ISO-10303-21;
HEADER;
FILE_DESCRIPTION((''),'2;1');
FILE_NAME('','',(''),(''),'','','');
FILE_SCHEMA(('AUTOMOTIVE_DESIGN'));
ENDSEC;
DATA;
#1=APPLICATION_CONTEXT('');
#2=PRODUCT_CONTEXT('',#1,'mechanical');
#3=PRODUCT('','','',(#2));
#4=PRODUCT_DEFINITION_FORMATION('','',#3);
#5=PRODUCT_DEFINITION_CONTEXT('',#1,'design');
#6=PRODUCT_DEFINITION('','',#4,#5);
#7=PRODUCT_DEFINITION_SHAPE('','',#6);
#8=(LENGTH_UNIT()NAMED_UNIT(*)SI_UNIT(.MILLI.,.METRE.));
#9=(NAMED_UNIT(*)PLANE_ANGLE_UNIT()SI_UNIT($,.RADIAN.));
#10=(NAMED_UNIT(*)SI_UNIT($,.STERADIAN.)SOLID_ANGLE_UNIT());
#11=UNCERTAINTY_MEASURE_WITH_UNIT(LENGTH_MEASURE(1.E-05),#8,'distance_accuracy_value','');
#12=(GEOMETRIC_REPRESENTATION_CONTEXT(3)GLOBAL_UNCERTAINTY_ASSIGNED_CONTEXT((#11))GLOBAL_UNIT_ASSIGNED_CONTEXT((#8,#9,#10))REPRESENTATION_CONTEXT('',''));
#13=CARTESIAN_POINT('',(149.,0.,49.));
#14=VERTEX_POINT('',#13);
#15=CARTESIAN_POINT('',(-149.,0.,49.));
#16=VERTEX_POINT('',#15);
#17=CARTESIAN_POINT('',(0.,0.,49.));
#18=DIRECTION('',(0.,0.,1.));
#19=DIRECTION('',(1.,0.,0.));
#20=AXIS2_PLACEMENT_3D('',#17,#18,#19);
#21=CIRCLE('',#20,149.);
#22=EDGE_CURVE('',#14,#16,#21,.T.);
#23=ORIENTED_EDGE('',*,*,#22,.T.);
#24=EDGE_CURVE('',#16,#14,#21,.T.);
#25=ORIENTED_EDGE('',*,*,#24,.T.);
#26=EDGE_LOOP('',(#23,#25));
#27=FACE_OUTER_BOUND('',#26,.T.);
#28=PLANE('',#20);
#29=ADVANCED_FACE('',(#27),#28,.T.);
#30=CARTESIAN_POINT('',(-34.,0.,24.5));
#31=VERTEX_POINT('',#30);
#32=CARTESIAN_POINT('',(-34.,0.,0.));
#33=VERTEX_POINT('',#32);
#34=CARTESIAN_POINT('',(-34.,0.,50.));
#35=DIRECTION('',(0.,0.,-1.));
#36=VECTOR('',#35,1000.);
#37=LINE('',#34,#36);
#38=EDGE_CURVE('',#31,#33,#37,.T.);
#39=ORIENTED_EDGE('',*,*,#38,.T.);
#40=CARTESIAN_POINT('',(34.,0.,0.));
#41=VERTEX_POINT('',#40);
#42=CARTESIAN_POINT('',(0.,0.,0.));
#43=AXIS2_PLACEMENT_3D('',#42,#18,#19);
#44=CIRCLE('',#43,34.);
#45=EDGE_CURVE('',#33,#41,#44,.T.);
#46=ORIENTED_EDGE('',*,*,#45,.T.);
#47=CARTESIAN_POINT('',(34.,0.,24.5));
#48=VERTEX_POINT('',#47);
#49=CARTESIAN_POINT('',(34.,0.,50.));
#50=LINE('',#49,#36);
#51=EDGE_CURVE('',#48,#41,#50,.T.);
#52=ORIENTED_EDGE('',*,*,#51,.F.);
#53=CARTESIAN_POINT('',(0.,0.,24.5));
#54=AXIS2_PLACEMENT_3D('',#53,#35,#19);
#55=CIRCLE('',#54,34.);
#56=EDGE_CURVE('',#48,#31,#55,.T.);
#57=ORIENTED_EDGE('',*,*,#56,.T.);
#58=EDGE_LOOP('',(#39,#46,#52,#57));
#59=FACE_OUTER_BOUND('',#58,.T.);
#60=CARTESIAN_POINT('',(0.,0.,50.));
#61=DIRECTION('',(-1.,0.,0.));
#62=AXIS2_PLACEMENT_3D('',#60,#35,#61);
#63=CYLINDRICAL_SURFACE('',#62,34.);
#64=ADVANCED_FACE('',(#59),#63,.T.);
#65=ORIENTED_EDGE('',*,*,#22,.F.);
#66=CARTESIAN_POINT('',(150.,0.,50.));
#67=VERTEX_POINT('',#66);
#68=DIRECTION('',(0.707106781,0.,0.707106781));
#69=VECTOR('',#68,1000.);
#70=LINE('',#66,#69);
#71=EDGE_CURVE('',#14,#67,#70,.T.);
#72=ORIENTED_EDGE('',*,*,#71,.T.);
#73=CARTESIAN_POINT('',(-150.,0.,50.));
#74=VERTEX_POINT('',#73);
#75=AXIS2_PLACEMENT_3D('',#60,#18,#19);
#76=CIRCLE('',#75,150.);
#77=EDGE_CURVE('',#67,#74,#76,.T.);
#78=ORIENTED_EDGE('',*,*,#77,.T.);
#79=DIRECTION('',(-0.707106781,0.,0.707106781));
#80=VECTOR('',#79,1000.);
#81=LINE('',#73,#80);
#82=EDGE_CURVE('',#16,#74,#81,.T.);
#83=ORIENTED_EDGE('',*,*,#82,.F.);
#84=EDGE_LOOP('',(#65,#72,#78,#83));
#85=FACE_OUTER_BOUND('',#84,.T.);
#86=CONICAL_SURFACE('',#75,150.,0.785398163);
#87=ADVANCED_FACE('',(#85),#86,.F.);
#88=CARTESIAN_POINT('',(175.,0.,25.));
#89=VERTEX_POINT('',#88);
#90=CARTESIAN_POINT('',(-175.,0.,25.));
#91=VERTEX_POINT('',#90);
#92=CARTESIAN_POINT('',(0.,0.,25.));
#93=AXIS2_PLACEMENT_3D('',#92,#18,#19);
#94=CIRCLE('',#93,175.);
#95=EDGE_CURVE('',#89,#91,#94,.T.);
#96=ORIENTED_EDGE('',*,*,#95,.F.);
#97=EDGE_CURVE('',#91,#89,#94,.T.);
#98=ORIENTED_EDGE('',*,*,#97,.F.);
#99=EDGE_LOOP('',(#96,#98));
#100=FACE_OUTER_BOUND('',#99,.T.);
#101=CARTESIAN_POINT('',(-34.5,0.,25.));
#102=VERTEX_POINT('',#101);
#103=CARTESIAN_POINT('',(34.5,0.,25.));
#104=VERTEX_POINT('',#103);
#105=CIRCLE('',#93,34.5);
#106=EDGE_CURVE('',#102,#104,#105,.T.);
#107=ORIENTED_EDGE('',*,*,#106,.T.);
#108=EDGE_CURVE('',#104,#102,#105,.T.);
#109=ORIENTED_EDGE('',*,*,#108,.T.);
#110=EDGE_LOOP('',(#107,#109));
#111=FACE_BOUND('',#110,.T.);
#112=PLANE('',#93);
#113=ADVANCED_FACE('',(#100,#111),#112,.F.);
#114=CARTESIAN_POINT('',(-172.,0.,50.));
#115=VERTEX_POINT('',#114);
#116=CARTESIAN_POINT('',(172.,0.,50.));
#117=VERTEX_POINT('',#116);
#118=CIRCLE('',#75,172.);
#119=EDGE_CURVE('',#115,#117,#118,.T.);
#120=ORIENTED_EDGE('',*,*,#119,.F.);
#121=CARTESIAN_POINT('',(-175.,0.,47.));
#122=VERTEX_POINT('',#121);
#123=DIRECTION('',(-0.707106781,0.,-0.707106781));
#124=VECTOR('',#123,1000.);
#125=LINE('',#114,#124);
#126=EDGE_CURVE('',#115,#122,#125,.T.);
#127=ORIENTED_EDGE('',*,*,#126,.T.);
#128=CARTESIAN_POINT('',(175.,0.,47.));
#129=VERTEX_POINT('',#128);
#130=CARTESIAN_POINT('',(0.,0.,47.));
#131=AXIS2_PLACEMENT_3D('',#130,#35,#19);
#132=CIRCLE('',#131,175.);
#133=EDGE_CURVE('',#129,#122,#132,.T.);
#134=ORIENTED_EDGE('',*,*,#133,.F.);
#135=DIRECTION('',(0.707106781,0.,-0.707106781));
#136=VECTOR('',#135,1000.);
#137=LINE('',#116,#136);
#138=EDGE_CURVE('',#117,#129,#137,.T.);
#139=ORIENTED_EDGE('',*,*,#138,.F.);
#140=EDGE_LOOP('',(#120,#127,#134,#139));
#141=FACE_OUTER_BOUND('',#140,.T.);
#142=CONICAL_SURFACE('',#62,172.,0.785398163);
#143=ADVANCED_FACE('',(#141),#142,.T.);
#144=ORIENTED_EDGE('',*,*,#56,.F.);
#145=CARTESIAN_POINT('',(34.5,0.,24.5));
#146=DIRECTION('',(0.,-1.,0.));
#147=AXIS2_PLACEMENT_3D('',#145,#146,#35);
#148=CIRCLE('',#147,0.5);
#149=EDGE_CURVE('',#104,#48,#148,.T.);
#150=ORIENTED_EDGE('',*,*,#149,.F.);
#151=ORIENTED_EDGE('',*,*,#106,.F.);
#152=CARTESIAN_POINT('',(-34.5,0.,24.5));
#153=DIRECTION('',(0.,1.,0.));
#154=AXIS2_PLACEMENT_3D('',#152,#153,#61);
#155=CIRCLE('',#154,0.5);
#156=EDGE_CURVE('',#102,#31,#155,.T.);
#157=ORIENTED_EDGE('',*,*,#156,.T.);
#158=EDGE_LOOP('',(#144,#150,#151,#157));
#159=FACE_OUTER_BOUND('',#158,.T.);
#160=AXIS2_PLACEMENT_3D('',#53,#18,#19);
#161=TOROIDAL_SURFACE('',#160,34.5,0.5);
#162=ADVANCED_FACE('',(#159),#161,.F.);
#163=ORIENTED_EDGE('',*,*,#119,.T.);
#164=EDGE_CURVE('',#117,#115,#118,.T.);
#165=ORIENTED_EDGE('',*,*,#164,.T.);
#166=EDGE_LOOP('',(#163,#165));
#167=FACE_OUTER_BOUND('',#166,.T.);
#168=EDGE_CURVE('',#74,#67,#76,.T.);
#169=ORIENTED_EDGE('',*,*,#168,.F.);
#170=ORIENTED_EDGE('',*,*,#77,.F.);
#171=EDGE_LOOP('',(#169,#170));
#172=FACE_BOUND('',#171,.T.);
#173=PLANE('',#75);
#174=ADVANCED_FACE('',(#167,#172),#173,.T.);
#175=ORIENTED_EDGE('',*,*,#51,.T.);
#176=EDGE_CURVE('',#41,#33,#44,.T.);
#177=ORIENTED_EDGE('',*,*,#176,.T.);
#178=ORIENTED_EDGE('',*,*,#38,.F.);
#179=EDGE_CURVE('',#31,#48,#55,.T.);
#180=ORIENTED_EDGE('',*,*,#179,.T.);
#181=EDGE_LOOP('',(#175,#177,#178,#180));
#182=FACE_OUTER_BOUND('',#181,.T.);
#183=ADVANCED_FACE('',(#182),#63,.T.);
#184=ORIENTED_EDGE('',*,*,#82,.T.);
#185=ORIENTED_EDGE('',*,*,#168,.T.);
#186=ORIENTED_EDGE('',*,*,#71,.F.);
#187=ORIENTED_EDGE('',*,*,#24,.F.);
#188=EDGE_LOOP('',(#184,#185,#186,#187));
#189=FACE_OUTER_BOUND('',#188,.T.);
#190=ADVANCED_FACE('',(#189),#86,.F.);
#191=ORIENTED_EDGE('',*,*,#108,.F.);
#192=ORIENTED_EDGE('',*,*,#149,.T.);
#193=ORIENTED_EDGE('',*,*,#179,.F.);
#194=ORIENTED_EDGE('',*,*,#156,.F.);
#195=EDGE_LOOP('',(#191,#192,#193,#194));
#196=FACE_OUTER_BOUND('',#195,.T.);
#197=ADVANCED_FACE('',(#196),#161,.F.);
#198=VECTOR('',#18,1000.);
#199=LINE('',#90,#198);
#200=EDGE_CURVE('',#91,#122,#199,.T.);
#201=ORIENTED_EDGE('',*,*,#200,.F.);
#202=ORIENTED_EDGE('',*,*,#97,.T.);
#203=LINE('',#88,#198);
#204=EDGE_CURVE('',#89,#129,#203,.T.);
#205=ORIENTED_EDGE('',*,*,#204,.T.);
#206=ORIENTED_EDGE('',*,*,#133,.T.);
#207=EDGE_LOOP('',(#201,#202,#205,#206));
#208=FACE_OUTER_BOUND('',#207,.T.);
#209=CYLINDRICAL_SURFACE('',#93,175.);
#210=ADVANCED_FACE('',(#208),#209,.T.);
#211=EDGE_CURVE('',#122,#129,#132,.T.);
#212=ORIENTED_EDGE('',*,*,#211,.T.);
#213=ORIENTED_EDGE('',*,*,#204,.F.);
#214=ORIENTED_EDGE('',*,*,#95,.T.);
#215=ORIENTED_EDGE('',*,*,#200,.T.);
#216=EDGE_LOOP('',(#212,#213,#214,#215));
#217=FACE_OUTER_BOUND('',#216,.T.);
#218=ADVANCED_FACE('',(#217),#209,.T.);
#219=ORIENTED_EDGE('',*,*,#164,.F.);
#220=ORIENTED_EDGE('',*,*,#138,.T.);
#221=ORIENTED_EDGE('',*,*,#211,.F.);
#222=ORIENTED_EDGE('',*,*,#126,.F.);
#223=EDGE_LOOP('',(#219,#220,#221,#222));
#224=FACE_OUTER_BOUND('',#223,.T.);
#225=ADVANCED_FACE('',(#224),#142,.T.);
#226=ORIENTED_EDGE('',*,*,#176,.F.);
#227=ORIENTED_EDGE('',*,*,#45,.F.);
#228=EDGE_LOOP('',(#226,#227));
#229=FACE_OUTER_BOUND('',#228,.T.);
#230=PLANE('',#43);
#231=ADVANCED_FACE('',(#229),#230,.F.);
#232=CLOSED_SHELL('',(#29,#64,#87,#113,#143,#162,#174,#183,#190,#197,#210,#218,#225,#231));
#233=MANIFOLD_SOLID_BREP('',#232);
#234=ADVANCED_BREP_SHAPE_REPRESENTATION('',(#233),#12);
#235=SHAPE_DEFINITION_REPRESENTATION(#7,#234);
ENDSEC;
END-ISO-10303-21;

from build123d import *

# Parameters (mm, degrees)
SKETCH1_R           = 34
BOSS_EXTRUDE1_DEPTH = 50
SKETCH2_R           = 175
BOSS_EXTRUDE2_DEPTH = 25
SKETCH3_R           = 150
CUT_EXTRUDE1_DEPTH  = 1
CUT_EXTRUDE1_DRAFT  = -45
FILLET1_R           = 0.5
CHAMFER1_SIZE       = 3


with BuildPart() as part:
    # Sketch1 → Boss-Extrude1 (new body)
    with BuildSketch(Plane.XY):
        Circle(SKETCH1_R)
    extrude(amount=BOSS_EXTRUDE1_DEPTH)

    # Sketch2 → Boss-Extrude2 (add)
    with BuildSketch(Plane.XY.offset(50)):
        Circle(SKETCH2_R)
    extrude(amount=-BOSS_EXTRUDE2_DEPTH)


with BuildPart() as cut_extrude1_tool:
    # Sketch3 → Cut-Extrude1 (with draft: the straight prism first)
    with BuildSketch(Plane.XY.offset(50)):
        Circle(SKETCH3_R)
    extrude(amount=-CUT_EXTRUDE1_DEPTH)
    # Cut-Extrude1: the draft: its side faces are tilted about the plane it starts from
    cut_extrude1_sides = [cut_extrude1_tool.faces().sort_by_distance(p)[0] for p in [
        (-150, 0, 49.5),
    ]]
    draft(cut_extrude1_sides, Plane.XY.offset(50), CUT_EXTRUDE1_DRAFT)


with BuildPart() as part_1:
    add(part.part)

    # Cut-Extrude1: cut by cut_extrude1_tool
    add(cut_extrude1_tool.part, mode=Mode.SUBTRACT)

    # Fillet1
    fillet1_edges = [part_1.edges().sort_by_distance(p)[0] for p in [
        (-34, 0, 25),
    ]]
    fillet(fillet1_edges, radius=FILLET1_R)

    # Chamfer1
    chamfer1_edges = [part_1.edges().sort_by_distance(p)[0] for p in [
        (-175, 0, 50),
    ]]
    chamfer(chamfer1_edges, length=CHAMFER1_SIZE)


solid = part_1.part
